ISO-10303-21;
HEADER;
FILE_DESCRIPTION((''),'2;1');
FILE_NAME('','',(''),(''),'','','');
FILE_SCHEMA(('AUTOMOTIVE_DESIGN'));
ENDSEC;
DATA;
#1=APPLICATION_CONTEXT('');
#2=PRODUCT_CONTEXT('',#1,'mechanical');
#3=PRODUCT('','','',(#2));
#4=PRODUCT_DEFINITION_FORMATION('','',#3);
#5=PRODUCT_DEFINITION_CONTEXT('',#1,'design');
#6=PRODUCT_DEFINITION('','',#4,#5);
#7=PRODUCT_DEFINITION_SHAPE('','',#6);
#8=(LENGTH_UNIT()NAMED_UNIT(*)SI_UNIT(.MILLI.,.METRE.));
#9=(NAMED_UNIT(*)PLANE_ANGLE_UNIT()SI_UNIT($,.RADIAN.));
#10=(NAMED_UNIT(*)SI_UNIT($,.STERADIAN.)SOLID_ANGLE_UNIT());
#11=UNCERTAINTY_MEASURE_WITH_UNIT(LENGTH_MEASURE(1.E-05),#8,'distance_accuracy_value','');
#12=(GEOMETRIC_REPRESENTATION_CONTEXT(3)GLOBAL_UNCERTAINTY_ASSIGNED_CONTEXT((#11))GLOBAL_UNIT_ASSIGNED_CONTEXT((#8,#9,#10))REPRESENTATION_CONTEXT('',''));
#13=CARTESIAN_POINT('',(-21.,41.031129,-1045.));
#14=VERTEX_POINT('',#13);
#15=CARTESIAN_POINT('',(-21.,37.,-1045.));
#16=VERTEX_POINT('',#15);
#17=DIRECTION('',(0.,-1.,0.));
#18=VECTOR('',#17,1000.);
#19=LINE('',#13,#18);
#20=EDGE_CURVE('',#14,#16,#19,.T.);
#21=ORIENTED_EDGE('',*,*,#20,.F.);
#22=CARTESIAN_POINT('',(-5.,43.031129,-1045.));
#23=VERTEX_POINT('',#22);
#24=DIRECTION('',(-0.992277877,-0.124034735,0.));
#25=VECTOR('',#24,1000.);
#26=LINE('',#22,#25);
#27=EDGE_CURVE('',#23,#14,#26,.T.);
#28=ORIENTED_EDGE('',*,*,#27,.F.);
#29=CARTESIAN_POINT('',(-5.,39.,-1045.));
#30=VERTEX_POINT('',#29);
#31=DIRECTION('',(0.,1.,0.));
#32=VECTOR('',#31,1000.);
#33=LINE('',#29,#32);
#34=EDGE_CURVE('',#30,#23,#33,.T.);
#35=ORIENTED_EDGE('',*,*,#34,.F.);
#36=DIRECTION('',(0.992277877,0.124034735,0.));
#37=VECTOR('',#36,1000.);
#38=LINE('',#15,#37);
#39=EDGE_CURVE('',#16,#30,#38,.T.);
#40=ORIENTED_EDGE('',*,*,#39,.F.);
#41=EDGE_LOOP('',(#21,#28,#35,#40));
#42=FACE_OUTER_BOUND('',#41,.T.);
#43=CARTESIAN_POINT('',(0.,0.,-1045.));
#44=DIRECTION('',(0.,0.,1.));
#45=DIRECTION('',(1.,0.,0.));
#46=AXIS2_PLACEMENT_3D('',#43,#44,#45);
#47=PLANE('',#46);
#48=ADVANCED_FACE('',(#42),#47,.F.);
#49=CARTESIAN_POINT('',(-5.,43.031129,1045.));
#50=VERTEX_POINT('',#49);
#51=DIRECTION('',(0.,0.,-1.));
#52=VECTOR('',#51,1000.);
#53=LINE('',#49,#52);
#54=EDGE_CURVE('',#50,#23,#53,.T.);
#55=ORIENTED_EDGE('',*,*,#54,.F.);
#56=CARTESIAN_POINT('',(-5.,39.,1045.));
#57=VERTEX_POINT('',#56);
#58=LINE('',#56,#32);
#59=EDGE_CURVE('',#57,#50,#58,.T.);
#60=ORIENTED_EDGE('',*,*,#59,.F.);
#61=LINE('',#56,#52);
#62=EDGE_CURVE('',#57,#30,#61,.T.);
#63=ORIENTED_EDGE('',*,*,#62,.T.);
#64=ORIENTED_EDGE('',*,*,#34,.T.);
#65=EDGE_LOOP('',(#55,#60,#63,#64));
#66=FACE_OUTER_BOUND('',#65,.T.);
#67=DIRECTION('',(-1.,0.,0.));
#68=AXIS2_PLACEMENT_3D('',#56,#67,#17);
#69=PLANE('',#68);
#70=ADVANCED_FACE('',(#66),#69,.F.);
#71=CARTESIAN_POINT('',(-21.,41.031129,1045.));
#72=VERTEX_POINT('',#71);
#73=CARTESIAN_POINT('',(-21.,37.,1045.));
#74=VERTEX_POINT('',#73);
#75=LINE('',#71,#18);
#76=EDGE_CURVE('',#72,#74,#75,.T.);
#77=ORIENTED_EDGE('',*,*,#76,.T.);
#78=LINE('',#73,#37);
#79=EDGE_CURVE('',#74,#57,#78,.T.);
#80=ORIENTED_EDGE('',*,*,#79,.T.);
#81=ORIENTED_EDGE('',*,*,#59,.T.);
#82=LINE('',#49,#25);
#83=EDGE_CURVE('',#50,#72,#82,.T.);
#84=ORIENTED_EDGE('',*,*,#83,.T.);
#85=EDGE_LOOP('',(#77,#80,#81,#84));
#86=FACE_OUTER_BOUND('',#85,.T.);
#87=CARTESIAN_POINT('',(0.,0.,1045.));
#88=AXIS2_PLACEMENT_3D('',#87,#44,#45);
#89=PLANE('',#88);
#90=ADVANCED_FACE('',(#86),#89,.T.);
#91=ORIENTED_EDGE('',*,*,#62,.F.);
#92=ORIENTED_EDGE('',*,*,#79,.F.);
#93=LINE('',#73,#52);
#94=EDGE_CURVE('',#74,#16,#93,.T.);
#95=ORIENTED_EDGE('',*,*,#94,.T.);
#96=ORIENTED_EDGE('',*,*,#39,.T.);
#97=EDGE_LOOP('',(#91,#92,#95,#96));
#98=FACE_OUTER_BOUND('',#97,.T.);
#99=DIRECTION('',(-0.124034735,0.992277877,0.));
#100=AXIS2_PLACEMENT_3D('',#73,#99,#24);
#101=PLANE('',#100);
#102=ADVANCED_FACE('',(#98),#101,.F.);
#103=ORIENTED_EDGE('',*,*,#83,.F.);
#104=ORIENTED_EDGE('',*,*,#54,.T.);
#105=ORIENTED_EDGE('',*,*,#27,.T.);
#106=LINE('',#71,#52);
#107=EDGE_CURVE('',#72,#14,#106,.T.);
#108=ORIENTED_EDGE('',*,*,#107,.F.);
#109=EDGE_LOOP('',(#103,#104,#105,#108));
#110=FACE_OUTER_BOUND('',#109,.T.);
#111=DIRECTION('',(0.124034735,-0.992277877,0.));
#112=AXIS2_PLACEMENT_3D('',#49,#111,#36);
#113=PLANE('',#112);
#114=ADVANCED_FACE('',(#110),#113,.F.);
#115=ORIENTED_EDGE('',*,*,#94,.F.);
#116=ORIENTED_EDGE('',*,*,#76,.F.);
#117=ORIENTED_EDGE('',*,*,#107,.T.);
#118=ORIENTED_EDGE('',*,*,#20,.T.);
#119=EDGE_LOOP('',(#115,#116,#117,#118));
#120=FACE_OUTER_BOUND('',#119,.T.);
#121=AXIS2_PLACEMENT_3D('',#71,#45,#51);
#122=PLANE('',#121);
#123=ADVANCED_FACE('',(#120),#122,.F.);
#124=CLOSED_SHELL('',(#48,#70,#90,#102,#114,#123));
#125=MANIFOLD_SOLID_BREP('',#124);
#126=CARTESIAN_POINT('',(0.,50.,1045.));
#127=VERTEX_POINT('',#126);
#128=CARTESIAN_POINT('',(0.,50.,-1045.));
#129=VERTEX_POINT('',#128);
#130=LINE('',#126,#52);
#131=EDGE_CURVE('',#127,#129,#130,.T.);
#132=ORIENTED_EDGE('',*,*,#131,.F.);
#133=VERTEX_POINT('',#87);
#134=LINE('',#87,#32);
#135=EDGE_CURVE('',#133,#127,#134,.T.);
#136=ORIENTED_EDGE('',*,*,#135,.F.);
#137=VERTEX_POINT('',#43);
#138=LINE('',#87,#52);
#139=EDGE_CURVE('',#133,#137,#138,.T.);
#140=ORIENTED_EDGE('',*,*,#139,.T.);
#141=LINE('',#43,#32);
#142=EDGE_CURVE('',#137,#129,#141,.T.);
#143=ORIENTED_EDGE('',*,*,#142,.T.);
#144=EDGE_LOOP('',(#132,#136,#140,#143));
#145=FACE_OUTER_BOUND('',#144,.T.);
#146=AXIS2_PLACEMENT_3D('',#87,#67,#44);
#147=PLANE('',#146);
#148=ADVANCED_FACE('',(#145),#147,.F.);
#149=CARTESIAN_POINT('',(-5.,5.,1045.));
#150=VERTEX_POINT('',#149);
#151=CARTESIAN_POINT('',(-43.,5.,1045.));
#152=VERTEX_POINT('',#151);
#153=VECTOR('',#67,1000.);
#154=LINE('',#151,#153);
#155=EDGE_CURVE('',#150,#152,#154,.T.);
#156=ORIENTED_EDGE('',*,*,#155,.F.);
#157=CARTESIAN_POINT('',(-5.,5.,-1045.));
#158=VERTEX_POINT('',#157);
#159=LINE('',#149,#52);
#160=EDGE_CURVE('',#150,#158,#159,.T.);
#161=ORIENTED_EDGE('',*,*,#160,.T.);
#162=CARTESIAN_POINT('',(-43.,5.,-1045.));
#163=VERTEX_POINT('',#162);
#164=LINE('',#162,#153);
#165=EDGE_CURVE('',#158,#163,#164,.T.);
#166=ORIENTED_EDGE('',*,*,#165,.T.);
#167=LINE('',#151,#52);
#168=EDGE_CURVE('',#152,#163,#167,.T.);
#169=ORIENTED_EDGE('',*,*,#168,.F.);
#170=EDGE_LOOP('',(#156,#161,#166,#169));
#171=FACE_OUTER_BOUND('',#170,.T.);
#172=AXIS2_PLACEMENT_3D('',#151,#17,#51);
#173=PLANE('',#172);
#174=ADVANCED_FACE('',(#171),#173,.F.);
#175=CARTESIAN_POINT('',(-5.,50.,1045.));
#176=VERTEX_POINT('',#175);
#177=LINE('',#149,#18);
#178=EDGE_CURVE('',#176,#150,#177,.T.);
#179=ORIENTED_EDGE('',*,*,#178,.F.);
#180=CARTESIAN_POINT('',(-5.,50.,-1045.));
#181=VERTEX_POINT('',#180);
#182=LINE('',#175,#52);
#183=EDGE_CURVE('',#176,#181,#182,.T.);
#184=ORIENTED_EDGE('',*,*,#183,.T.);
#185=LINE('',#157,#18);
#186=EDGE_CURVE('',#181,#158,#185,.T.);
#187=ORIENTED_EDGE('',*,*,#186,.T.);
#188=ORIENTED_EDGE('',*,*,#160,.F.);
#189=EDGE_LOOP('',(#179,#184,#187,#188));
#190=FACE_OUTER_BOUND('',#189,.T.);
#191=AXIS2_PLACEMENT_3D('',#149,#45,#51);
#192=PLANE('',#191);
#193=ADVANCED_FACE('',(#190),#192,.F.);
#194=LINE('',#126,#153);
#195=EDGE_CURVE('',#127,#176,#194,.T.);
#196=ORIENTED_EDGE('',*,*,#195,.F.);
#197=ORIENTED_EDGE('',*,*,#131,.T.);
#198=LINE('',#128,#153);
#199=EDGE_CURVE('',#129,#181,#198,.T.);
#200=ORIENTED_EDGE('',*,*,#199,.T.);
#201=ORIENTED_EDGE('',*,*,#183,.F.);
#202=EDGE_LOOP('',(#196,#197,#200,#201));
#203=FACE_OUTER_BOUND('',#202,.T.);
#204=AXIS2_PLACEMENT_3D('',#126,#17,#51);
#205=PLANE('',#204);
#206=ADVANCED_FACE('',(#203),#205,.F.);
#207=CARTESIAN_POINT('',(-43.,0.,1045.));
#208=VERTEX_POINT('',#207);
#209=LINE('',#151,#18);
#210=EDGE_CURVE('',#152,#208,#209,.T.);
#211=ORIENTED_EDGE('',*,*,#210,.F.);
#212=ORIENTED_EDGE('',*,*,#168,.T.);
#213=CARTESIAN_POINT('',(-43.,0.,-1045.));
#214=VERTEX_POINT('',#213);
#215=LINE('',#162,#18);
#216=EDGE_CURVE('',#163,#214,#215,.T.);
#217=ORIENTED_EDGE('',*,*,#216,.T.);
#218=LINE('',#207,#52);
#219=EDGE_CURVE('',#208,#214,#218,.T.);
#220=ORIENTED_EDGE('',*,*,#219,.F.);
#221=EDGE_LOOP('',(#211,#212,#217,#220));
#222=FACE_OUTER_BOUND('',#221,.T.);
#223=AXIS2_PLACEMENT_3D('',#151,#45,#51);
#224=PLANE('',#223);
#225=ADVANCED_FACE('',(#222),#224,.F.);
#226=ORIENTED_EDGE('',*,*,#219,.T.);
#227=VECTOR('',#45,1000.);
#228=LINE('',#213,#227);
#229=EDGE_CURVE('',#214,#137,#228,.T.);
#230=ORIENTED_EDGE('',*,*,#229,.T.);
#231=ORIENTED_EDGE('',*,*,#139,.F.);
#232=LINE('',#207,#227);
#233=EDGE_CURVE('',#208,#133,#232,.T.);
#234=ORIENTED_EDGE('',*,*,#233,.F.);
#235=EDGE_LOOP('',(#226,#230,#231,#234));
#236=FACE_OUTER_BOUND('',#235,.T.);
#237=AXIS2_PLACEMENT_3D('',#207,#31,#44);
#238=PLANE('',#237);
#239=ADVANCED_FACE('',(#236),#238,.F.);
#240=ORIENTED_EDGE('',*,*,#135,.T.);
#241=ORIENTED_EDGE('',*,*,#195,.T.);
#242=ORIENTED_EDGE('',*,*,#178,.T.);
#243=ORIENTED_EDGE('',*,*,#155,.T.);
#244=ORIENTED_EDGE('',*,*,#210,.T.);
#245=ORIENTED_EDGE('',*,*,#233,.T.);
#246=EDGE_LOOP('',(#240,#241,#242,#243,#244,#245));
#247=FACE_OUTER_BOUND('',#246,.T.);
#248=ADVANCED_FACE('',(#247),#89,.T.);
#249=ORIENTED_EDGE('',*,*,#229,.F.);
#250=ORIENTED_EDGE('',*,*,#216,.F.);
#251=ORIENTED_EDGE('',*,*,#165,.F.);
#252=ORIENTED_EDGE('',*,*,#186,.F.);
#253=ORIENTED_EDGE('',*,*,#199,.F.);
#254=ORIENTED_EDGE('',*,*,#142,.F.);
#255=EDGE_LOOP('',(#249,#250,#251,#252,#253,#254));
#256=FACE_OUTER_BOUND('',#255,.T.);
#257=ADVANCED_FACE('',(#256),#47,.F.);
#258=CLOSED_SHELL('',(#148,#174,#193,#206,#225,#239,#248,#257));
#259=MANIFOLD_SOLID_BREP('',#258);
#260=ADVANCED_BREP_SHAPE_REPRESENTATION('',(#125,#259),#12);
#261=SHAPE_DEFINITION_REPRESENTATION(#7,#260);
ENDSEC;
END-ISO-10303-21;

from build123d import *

# Parameters (mm, degrees)
EXTRUDE_1_DEPTH = 1045
EXTRUDE_2_DEPTH = 1045


with BuildPart() as part:
    # 草图1 → 凸台-拉伸1 (new, symmetric)
    with BuildSketch(Plane.XY):
        Polygon((-43, 0), (0, 0), (0, 50), (-5, 50), (-5, 5), (-43, 5), align=None)
    extrude(amount=EXTRUDE_1_DEPTH, both=True)


with BuildPart() as body_2:
    # 草图2 → 凸台-拉伸2 (new, symmetric)
    with BuildSketch(Plane.XY):
        Polygon((-5, 43.031128874), (-21, 41.031128874), (-21, 37), (-5, 39), align=None)
    extrude(amount=EXTRUDE_2_DEPTH, both=True)


solid = Compound([part.part, body_2.part])
